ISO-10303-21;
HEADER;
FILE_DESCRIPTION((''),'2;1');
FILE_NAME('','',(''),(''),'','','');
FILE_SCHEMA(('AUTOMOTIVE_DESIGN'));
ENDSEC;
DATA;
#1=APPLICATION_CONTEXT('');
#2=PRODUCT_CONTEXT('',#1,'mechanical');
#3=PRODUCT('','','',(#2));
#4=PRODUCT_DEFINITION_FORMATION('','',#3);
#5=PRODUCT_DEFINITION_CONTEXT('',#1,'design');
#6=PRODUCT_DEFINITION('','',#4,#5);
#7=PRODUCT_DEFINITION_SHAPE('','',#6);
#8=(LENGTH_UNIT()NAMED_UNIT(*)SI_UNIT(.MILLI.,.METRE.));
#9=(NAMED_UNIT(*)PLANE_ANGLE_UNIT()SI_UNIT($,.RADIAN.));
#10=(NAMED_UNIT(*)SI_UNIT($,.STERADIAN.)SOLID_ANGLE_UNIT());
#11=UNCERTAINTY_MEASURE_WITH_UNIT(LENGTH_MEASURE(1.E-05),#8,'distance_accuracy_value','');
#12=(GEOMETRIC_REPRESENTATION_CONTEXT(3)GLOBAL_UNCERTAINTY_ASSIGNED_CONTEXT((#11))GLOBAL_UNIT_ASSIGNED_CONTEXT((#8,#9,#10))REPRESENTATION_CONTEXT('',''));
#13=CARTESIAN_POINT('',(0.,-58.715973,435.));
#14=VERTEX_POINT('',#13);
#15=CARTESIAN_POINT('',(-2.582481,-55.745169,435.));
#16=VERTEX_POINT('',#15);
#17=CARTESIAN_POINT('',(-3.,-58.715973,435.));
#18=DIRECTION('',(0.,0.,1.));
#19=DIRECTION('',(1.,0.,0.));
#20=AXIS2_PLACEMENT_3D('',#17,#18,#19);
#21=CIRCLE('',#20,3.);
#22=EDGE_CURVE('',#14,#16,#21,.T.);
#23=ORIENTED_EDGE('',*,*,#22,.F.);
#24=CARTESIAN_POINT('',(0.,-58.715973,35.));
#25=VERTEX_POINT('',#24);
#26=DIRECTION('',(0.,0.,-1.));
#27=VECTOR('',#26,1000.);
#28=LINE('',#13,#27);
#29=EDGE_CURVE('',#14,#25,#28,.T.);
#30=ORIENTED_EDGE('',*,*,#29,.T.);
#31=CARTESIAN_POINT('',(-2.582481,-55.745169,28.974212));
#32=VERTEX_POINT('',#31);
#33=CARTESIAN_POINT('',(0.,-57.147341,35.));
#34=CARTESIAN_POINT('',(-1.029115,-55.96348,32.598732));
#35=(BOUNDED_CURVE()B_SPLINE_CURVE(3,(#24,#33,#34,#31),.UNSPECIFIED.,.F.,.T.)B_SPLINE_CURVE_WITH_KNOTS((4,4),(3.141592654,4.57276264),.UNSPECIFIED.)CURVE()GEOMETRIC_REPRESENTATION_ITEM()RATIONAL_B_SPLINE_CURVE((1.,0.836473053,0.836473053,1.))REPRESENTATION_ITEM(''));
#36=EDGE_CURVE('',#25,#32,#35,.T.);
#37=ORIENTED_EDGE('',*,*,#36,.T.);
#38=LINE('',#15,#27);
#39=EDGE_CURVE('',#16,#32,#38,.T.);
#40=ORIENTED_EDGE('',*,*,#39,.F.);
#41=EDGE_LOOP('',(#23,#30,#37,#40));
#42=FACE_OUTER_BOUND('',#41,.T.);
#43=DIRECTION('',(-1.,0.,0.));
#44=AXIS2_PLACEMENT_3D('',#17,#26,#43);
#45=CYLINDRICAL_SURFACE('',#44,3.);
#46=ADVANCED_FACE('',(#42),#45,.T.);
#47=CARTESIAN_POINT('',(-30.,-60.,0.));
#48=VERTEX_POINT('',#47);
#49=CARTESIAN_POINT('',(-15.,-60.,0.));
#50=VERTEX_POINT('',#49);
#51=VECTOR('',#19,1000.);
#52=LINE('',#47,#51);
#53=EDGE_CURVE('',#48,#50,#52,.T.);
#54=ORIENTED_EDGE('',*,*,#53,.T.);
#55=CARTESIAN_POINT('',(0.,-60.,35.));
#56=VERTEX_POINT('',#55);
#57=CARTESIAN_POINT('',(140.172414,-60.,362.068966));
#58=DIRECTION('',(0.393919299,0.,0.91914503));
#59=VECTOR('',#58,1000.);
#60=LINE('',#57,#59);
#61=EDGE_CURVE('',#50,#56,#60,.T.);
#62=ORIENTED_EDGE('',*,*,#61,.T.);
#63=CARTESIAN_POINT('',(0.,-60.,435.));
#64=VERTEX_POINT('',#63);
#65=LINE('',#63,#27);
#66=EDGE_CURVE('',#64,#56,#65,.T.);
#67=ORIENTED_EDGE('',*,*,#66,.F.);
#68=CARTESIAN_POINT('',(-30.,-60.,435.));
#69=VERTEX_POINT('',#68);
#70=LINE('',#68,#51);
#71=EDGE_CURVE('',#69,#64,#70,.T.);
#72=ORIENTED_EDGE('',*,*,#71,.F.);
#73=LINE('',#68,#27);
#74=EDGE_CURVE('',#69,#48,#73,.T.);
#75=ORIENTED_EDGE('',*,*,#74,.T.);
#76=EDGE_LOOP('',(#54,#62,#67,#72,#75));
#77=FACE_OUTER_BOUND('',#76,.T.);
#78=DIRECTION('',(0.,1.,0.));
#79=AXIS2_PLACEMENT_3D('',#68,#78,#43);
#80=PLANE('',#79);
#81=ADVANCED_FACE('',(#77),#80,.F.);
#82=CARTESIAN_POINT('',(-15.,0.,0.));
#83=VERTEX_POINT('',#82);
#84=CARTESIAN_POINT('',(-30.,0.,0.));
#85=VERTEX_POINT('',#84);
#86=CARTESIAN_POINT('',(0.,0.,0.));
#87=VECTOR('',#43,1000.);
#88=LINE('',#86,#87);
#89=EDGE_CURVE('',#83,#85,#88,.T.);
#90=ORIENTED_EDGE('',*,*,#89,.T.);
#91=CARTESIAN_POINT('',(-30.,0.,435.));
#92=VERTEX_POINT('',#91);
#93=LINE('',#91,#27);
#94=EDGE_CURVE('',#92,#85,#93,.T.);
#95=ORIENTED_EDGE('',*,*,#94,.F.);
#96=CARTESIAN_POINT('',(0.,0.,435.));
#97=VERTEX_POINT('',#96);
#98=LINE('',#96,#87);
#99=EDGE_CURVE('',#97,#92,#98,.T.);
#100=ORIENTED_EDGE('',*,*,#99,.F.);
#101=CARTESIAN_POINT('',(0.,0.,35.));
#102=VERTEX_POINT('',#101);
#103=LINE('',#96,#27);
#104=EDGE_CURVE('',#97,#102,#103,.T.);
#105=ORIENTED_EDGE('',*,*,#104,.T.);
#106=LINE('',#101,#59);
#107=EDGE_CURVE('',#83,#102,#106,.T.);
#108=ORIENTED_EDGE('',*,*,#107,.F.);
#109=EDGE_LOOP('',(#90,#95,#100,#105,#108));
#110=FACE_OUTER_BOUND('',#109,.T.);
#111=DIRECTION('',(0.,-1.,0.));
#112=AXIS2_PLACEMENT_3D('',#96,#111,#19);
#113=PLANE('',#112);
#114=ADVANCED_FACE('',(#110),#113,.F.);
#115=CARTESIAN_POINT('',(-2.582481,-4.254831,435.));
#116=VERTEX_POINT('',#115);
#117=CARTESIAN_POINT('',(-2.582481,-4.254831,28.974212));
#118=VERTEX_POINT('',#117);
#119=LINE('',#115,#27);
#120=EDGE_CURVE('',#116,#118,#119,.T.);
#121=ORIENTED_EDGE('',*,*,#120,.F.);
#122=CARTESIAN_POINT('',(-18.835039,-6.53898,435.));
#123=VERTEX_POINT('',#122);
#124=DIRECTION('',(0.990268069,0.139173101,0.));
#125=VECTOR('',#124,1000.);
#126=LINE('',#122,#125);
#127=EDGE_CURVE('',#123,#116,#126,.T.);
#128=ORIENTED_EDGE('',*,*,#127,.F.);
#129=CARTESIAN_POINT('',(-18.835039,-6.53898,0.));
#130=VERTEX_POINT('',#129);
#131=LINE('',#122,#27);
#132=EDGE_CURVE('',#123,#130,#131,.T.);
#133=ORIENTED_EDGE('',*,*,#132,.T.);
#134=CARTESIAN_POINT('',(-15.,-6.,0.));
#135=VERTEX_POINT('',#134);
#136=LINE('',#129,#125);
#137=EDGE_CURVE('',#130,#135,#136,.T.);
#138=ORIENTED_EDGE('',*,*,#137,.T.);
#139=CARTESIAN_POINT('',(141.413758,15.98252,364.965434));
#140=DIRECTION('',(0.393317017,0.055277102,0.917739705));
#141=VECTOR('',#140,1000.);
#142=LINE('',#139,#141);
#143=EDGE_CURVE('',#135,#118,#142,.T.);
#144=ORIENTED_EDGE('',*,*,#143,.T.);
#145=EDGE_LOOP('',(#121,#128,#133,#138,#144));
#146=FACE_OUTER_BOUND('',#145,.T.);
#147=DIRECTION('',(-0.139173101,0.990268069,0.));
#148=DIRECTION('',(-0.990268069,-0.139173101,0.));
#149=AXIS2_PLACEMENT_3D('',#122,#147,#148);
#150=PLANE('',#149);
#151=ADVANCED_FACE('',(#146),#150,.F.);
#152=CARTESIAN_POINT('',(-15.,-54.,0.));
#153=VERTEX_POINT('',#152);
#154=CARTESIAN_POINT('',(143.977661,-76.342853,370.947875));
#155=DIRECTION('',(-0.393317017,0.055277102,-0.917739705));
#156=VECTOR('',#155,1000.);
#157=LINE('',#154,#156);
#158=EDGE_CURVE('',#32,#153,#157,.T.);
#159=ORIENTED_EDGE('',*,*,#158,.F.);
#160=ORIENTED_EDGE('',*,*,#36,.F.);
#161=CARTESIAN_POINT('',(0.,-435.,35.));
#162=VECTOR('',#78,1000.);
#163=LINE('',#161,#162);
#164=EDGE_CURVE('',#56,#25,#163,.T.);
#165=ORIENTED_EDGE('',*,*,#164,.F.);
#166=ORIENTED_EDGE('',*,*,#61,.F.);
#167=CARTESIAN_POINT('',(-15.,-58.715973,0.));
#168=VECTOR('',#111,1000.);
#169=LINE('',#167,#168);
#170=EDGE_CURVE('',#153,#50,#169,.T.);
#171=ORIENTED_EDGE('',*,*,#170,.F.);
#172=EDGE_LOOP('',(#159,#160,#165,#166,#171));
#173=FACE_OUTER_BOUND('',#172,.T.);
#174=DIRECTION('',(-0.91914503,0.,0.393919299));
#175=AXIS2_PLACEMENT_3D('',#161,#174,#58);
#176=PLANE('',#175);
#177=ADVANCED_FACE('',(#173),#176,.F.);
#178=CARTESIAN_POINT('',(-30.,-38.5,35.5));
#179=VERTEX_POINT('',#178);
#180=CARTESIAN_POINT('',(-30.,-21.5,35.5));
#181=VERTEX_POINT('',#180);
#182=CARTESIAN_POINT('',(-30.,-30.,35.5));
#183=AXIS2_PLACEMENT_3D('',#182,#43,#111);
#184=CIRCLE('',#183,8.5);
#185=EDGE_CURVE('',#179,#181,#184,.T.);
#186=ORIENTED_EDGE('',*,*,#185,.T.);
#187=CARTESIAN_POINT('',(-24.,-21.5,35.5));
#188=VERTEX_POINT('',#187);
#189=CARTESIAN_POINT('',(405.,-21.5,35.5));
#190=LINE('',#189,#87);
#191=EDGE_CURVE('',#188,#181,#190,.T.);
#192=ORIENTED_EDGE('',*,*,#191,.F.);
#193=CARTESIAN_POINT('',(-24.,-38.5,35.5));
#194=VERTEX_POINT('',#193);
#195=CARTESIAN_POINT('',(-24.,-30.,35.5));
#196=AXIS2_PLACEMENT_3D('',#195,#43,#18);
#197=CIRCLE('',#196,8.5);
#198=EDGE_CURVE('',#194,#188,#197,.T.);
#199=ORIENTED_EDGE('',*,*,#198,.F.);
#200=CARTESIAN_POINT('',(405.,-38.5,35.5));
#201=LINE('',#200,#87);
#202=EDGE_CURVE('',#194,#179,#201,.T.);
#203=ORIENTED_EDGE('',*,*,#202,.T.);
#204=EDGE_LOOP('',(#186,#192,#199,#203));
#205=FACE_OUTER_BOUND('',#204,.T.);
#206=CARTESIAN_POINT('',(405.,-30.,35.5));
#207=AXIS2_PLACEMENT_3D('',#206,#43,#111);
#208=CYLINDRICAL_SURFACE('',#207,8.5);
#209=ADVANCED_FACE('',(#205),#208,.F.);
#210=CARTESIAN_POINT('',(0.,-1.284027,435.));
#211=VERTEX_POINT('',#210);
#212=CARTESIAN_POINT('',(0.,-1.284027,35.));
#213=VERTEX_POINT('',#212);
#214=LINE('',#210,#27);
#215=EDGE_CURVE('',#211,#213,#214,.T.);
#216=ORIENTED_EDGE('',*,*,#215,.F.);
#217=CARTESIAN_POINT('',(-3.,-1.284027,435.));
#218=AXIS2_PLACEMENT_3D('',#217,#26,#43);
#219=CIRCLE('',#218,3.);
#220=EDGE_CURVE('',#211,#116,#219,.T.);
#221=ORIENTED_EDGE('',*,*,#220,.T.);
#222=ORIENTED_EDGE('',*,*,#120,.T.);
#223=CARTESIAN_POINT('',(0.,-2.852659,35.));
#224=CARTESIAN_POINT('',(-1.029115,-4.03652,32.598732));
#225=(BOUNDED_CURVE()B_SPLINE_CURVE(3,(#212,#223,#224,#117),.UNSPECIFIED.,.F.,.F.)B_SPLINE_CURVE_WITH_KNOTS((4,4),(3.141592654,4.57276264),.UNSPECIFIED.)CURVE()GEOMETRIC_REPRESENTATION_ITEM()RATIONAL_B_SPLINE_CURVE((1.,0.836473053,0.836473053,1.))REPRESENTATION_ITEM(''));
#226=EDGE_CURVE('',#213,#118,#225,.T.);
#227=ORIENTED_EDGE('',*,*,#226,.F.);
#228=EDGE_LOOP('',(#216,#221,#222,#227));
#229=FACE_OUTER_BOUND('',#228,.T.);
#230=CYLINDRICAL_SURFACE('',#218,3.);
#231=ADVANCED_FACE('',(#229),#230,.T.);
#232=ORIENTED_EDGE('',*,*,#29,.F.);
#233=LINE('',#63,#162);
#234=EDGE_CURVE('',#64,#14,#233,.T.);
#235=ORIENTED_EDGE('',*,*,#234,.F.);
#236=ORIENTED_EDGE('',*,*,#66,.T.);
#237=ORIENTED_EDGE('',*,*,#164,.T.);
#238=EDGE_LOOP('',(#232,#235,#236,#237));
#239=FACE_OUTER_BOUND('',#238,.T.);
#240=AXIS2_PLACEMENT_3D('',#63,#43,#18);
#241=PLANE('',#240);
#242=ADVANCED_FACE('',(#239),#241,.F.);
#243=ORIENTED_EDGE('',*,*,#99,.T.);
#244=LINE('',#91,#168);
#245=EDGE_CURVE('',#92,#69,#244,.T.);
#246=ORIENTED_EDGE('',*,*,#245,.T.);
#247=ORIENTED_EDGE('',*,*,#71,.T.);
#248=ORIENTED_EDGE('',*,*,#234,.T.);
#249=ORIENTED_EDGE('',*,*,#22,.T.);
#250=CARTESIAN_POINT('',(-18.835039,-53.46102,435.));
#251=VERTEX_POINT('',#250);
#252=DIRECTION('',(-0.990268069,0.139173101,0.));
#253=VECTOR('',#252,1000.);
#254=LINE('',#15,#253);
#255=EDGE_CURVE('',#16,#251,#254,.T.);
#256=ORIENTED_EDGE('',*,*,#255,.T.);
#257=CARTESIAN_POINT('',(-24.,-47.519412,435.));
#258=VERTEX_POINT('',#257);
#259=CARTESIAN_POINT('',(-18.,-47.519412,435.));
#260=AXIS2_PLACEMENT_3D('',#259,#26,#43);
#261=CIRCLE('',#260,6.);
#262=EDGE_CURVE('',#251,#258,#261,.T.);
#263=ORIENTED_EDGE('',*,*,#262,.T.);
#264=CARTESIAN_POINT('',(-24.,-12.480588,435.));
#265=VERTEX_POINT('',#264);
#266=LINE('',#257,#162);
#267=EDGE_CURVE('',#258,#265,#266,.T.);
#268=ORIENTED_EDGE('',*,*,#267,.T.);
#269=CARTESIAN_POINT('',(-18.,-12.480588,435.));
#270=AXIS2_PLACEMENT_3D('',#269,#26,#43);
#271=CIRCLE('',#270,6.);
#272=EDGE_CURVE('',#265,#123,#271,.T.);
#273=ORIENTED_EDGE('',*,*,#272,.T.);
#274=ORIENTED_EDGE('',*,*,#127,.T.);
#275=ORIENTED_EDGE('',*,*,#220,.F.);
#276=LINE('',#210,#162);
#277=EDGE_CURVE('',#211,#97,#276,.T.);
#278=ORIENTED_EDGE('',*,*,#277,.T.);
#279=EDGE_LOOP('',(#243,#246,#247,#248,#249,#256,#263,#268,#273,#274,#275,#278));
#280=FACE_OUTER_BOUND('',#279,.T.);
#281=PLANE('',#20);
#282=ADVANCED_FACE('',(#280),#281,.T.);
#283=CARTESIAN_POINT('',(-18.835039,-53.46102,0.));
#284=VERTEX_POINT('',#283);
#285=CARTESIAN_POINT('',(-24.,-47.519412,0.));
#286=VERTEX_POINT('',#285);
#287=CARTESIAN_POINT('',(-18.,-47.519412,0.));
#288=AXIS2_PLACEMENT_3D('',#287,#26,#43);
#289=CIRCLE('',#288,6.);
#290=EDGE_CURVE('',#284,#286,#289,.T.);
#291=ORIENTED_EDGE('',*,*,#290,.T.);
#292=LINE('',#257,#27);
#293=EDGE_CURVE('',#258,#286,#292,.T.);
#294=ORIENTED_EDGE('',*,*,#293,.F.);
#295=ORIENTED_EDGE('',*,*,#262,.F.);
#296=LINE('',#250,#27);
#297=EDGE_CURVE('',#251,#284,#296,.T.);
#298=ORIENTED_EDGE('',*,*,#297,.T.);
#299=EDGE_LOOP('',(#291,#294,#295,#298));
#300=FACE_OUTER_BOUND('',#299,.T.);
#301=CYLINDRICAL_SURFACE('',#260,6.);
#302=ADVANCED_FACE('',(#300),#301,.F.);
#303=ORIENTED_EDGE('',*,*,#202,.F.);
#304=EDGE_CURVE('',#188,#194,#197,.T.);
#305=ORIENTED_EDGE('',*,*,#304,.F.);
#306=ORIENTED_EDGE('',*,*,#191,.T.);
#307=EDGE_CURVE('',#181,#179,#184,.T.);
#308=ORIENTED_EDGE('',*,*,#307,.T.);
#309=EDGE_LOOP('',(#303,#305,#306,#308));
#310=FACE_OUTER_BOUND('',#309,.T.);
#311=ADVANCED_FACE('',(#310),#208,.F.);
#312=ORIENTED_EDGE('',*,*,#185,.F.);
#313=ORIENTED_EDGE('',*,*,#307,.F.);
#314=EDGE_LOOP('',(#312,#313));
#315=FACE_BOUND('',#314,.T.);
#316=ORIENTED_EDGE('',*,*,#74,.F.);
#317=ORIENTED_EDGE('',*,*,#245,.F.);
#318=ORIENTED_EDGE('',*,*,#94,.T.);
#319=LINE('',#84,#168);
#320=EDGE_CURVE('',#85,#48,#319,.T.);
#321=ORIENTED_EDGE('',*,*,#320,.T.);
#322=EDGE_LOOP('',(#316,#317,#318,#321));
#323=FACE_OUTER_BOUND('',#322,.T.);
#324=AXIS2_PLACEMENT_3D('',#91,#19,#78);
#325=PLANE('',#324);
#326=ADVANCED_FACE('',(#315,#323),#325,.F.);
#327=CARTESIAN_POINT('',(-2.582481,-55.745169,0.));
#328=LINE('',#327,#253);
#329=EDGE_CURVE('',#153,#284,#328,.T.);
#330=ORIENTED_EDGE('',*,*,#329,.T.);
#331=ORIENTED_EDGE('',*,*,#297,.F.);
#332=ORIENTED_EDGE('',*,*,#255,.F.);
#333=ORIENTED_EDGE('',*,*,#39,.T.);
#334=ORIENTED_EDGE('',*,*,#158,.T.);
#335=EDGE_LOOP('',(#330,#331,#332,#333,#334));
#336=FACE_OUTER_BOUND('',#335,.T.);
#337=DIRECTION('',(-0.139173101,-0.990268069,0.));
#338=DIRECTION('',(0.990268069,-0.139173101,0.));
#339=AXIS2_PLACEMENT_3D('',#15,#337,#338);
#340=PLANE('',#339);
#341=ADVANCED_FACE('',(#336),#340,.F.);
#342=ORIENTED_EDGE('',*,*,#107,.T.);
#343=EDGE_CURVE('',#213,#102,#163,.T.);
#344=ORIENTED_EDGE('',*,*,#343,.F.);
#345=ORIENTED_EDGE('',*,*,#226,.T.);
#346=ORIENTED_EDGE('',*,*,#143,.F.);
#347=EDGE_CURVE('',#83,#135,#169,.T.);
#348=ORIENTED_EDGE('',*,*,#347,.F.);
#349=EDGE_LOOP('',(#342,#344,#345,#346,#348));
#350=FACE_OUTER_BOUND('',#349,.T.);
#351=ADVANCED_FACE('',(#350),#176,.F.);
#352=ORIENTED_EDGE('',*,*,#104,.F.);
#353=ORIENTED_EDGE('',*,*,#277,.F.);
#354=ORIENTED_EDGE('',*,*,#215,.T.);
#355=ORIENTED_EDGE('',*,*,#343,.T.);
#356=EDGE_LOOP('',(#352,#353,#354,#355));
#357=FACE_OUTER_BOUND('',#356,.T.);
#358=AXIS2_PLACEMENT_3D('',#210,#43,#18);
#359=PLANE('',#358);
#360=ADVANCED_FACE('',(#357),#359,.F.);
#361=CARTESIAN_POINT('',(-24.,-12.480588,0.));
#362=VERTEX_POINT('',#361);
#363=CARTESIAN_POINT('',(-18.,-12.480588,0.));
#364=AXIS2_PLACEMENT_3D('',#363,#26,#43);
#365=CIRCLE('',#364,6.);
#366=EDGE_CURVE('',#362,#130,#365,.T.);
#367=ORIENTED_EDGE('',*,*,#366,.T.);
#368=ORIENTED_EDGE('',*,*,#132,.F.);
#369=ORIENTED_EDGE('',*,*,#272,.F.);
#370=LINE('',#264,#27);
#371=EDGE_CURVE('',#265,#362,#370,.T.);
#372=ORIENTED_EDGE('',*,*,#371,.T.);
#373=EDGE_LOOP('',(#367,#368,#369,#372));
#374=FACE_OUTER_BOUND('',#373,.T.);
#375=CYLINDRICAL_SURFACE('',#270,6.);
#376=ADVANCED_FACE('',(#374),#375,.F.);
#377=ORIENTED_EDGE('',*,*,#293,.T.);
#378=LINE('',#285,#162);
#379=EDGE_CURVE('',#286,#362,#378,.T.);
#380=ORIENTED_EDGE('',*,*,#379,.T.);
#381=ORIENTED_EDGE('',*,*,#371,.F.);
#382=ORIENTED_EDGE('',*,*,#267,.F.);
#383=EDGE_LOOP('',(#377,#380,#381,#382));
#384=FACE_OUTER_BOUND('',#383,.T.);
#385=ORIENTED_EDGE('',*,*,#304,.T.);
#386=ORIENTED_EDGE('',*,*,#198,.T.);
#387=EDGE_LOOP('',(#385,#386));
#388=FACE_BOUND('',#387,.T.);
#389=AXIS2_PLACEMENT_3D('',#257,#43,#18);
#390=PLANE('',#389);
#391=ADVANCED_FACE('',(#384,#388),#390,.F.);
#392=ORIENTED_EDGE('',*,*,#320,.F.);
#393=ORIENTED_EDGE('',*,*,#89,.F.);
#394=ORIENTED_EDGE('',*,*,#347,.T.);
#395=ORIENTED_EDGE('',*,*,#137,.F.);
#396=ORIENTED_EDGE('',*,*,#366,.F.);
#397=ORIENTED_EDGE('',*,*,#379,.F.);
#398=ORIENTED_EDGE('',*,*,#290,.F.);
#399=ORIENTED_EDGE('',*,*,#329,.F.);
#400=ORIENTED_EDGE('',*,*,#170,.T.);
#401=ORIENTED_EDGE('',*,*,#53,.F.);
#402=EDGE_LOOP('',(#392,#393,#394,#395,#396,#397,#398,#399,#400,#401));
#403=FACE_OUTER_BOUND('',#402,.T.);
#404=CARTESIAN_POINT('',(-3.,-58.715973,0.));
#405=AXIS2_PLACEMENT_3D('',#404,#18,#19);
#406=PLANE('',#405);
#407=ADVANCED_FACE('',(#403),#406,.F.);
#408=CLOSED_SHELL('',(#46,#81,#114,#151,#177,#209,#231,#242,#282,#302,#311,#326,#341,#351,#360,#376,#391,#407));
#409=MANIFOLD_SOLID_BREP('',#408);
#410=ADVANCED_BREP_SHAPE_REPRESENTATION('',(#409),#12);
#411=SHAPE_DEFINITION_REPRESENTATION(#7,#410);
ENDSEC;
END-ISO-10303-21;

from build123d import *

# Parameters (mm, degrees)
BOSS_EXTRUDE1_DEPTH = 435
SKETCH2_R           = 8.5
CUT_EXTRUDE1_DEPTH  = 435
CUT_EXTRUDE2_DEPTH  = 435


with BuildPart() as part:
    # Sketch1 → Boss-Extrude1 (new body)
    with BuildSketch(Plane.XY):
        with BuildLine():
            Line((0, 0), (-30, 0))
            Line((-30, 0), (-30, -60))
            Line((-30, -60), (0, -60))
            Line((0, -60), (0, -58.715972734))
            ThreePointArc((0, -58.715972734), (-0.735871259, -56.747795647), (-2.582480697, -55.745168528))
            Line((-2.582480697, -55.745168528), (-18.835038606, -53.461020473))
            ThreePointArc((-18.835038606, -53.461020473), (-22.528257481, -51.455766235), (-24, -47.519412061))
            Line((-24, -47.519412061), (-24, -12.480587939))
            ThreePointArc((-24, -12.480587939), (-22.528257481, -8.544233765), (-18.835038606, -6.538979527))
            Line((-18.835038606, -6.538979527), (-2.582480697, -4.254831472))
            ThreePointArc((-2.582480697, -4.254831472), (-0.735871259, -3.252204353), (0, -1.284027266))
            Line((0, -1.284027266), (0, 0))
        make_face()
    extrude(amount=BOSS_EXTRUDE1_DEPTH)

    # Sketch2 → Cut-Extrude1 (cut)
    with BuildSketch(Plane.ZY.offset(30)):
        with Locations(Location((35.5, -30, 0), (0, 0, 270))):
            Circle(SKETCH2_R)
    extrude(amount=-CUT_EXTRUDE1_DEPTH, mode=Mode.SUBTRACT)

    # Sketch3 → Cut-Extrude2 (cut)
    with BuildSketch(Plane(origin=(0, 0, 0), x_dir=(1, 0, 0), z_dir=(0, 1, 0))):
        Polygon((-15, 0), (0, 0), (0, -35), align=None)
    extrude(amount=-CUT_EXTRUDE2_DEPTH, mode=Mode.SUBTRACT)


solid = part.part
